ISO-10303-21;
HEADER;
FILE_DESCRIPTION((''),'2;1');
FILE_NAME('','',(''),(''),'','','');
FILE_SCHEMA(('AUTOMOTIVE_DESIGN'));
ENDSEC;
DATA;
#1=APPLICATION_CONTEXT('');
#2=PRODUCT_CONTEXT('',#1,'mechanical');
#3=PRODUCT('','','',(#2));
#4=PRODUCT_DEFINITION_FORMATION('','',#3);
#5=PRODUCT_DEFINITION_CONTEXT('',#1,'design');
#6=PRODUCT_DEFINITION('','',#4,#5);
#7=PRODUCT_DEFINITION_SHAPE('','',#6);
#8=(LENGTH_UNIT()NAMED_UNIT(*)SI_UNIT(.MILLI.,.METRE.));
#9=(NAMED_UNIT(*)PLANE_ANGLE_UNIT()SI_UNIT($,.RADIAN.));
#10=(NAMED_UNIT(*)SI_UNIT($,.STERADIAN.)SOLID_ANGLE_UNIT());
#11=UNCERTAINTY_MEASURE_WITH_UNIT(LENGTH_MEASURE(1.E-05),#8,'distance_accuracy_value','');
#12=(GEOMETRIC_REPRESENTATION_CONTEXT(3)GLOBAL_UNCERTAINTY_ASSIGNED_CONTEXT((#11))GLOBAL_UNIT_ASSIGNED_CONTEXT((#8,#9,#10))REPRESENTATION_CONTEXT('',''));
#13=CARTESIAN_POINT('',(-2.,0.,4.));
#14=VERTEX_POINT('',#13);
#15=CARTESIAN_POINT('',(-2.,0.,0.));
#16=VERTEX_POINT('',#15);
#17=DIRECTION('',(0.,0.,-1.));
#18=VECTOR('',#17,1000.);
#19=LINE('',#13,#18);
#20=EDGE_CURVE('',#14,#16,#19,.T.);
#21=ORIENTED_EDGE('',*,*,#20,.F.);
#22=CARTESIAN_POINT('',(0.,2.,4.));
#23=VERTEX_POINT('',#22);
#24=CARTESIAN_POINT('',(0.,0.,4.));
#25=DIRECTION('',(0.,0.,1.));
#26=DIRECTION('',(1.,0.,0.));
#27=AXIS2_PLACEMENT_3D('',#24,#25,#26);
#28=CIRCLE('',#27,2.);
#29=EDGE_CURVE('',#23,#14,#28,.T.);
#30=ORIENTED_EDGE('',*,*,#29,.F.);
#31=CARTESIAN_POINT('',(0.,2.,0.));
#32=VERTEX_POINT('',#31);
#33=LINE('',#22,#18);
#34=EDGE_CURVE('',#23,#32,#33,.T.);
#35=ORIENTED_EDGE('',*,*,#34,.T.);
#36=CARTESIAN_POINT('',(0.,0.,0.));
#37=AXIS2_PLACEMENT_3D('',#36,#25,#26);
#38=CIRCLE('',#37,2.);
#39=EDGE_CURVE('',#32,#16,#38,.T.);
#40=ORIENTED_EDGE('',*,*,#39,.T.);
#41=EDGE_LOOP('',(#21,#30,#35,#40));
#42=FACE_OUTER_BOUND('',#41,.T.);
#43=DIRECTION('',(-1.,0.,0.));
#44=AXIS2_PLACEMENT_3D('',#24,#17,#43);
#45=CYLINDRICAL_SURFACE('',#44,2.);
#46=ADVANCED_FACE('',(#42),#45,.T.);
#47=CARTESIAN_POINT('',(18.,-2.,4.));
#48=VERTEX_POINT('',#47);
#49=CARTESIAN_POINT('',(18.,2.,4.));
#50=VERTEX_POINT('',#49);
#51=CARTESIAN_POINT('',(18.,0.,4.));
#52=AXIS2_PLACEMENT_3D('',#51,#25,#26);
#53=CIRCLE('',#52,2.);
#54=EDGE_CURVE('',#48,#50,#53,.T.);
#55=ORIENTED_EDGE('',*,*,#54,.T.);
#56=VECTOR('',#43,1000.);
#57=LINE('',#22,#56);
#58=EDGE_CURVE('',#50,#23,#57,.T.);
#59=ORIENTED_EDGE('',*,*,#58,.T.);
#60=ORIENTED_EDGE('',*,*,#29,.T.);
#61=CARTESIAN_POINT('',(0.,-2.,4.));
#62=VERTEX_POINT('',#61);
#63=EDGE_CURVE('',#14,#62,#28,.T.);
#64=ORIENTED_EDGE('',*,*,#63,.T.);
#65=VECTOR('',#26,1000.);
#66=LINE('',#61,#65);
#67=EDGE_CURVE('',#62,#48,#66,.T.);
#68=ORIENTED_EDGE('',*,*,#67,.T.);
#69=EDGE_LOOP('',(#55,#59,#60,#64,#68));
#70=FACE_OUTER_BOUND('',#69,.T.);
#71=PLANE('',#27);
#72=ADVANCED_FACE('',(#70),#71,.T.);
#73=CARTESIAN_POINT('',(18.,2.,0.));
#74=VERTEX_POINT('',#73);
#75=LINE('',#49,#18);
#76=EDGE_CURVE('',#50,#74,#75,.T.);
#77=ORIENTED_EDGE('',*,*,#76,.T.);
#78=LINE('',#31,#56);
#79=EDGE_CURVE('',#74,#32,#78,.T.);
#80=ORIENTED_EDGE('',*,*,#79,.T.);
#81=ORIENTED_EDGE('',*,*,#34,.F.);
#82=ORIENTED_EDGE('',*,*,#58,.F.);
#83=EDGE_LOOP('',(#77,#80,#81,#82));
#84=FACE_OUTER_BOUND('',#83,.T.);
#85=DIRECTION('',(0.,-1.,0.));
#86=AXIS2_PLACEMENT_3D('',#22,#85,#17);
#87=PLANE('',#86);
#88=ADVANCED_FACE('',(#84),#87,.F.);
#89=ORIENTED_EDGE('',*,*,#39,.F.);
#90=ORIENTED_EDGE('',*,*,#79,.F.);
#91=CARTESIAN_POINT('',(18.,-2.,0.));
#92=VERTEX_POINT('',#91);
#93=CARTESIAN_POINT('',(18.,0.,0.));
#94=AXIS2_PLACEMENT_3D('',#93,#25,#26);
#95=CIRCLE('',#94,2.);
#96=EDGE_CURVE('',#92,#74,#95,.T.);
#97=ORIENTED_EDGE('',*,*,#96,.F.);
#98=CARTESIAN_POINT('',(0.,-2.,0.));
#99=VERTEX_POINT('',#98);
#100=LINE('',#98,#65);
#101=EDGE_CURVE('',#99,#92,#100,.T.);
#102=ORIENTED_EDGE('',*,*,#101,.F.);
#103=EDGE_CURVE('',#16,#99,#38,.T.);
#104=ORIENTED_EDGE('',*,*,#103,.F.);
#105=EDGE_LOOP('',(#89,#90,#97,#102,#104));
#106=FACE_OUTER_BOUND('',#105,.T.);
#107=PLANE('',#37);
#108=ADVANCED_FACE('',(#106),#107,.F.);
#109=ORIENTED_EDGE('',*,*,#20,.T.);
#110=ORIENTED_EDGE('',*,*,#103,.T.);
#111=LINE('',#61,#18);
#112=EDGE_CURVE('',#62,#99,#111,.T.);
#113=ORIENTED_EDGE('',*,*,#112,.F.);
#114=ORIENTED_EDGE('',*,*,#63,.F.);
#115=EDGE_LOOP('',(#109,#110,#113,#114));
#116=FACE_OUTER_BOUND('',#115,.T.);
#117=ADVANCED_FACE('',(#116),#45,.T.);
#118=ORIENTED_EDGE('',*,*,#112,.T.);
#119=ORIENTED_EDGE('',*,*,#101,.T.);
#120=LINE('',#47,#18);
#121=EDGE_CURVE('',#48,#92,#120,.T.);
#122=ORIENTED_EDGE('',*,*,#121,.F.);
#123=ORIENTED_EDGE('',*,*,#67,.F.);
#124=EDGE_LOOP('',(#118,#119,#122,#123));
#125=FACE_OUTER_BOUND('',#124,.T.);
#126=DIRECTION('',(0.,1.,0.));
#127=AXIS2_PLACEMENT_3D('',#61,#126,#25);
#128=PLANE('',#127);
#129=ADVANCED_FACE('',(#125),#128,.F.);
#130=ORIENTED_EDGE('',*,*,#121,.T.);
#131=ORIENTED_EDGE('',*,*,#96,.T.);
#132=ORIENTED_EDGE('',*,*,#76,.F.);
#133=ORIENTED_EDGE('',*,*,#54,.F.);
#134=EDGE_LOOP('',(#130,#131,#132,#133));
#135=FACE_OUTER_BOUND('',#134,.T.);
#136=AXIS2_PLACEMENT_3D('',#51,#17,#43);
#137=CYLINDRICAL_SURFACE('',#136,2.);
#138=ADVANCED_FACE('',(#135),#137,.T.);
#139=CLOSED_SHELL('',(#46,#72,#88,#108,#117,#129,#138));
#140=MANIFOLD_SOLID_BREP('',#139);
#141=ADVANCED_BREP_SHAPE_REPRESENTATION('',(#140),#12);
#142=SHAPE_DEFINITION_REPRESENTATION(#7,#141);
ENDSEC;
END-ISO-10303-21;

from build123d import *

# Parameters (mm, degrees)
BOSS_EXTRUDE1_DEPTH = 4


with BuildPart() as part:
    # Sketch1 → Boss-Extrude1 (new body)
    with BuildSketch(Plane.XY):
        with BuildLine():
            Line((0, 2), (18, 2))
            ThreePointArc((18, 2), (20, 0), (18, -2))
            Line((18, -2), (0, -2))
            ThreePointArc((0, -2), (-2, 0), (0, 2))
        make_face()
    extrude(amount=BOSS_EXTRUDE1_DEPTH)


solid = part.part
